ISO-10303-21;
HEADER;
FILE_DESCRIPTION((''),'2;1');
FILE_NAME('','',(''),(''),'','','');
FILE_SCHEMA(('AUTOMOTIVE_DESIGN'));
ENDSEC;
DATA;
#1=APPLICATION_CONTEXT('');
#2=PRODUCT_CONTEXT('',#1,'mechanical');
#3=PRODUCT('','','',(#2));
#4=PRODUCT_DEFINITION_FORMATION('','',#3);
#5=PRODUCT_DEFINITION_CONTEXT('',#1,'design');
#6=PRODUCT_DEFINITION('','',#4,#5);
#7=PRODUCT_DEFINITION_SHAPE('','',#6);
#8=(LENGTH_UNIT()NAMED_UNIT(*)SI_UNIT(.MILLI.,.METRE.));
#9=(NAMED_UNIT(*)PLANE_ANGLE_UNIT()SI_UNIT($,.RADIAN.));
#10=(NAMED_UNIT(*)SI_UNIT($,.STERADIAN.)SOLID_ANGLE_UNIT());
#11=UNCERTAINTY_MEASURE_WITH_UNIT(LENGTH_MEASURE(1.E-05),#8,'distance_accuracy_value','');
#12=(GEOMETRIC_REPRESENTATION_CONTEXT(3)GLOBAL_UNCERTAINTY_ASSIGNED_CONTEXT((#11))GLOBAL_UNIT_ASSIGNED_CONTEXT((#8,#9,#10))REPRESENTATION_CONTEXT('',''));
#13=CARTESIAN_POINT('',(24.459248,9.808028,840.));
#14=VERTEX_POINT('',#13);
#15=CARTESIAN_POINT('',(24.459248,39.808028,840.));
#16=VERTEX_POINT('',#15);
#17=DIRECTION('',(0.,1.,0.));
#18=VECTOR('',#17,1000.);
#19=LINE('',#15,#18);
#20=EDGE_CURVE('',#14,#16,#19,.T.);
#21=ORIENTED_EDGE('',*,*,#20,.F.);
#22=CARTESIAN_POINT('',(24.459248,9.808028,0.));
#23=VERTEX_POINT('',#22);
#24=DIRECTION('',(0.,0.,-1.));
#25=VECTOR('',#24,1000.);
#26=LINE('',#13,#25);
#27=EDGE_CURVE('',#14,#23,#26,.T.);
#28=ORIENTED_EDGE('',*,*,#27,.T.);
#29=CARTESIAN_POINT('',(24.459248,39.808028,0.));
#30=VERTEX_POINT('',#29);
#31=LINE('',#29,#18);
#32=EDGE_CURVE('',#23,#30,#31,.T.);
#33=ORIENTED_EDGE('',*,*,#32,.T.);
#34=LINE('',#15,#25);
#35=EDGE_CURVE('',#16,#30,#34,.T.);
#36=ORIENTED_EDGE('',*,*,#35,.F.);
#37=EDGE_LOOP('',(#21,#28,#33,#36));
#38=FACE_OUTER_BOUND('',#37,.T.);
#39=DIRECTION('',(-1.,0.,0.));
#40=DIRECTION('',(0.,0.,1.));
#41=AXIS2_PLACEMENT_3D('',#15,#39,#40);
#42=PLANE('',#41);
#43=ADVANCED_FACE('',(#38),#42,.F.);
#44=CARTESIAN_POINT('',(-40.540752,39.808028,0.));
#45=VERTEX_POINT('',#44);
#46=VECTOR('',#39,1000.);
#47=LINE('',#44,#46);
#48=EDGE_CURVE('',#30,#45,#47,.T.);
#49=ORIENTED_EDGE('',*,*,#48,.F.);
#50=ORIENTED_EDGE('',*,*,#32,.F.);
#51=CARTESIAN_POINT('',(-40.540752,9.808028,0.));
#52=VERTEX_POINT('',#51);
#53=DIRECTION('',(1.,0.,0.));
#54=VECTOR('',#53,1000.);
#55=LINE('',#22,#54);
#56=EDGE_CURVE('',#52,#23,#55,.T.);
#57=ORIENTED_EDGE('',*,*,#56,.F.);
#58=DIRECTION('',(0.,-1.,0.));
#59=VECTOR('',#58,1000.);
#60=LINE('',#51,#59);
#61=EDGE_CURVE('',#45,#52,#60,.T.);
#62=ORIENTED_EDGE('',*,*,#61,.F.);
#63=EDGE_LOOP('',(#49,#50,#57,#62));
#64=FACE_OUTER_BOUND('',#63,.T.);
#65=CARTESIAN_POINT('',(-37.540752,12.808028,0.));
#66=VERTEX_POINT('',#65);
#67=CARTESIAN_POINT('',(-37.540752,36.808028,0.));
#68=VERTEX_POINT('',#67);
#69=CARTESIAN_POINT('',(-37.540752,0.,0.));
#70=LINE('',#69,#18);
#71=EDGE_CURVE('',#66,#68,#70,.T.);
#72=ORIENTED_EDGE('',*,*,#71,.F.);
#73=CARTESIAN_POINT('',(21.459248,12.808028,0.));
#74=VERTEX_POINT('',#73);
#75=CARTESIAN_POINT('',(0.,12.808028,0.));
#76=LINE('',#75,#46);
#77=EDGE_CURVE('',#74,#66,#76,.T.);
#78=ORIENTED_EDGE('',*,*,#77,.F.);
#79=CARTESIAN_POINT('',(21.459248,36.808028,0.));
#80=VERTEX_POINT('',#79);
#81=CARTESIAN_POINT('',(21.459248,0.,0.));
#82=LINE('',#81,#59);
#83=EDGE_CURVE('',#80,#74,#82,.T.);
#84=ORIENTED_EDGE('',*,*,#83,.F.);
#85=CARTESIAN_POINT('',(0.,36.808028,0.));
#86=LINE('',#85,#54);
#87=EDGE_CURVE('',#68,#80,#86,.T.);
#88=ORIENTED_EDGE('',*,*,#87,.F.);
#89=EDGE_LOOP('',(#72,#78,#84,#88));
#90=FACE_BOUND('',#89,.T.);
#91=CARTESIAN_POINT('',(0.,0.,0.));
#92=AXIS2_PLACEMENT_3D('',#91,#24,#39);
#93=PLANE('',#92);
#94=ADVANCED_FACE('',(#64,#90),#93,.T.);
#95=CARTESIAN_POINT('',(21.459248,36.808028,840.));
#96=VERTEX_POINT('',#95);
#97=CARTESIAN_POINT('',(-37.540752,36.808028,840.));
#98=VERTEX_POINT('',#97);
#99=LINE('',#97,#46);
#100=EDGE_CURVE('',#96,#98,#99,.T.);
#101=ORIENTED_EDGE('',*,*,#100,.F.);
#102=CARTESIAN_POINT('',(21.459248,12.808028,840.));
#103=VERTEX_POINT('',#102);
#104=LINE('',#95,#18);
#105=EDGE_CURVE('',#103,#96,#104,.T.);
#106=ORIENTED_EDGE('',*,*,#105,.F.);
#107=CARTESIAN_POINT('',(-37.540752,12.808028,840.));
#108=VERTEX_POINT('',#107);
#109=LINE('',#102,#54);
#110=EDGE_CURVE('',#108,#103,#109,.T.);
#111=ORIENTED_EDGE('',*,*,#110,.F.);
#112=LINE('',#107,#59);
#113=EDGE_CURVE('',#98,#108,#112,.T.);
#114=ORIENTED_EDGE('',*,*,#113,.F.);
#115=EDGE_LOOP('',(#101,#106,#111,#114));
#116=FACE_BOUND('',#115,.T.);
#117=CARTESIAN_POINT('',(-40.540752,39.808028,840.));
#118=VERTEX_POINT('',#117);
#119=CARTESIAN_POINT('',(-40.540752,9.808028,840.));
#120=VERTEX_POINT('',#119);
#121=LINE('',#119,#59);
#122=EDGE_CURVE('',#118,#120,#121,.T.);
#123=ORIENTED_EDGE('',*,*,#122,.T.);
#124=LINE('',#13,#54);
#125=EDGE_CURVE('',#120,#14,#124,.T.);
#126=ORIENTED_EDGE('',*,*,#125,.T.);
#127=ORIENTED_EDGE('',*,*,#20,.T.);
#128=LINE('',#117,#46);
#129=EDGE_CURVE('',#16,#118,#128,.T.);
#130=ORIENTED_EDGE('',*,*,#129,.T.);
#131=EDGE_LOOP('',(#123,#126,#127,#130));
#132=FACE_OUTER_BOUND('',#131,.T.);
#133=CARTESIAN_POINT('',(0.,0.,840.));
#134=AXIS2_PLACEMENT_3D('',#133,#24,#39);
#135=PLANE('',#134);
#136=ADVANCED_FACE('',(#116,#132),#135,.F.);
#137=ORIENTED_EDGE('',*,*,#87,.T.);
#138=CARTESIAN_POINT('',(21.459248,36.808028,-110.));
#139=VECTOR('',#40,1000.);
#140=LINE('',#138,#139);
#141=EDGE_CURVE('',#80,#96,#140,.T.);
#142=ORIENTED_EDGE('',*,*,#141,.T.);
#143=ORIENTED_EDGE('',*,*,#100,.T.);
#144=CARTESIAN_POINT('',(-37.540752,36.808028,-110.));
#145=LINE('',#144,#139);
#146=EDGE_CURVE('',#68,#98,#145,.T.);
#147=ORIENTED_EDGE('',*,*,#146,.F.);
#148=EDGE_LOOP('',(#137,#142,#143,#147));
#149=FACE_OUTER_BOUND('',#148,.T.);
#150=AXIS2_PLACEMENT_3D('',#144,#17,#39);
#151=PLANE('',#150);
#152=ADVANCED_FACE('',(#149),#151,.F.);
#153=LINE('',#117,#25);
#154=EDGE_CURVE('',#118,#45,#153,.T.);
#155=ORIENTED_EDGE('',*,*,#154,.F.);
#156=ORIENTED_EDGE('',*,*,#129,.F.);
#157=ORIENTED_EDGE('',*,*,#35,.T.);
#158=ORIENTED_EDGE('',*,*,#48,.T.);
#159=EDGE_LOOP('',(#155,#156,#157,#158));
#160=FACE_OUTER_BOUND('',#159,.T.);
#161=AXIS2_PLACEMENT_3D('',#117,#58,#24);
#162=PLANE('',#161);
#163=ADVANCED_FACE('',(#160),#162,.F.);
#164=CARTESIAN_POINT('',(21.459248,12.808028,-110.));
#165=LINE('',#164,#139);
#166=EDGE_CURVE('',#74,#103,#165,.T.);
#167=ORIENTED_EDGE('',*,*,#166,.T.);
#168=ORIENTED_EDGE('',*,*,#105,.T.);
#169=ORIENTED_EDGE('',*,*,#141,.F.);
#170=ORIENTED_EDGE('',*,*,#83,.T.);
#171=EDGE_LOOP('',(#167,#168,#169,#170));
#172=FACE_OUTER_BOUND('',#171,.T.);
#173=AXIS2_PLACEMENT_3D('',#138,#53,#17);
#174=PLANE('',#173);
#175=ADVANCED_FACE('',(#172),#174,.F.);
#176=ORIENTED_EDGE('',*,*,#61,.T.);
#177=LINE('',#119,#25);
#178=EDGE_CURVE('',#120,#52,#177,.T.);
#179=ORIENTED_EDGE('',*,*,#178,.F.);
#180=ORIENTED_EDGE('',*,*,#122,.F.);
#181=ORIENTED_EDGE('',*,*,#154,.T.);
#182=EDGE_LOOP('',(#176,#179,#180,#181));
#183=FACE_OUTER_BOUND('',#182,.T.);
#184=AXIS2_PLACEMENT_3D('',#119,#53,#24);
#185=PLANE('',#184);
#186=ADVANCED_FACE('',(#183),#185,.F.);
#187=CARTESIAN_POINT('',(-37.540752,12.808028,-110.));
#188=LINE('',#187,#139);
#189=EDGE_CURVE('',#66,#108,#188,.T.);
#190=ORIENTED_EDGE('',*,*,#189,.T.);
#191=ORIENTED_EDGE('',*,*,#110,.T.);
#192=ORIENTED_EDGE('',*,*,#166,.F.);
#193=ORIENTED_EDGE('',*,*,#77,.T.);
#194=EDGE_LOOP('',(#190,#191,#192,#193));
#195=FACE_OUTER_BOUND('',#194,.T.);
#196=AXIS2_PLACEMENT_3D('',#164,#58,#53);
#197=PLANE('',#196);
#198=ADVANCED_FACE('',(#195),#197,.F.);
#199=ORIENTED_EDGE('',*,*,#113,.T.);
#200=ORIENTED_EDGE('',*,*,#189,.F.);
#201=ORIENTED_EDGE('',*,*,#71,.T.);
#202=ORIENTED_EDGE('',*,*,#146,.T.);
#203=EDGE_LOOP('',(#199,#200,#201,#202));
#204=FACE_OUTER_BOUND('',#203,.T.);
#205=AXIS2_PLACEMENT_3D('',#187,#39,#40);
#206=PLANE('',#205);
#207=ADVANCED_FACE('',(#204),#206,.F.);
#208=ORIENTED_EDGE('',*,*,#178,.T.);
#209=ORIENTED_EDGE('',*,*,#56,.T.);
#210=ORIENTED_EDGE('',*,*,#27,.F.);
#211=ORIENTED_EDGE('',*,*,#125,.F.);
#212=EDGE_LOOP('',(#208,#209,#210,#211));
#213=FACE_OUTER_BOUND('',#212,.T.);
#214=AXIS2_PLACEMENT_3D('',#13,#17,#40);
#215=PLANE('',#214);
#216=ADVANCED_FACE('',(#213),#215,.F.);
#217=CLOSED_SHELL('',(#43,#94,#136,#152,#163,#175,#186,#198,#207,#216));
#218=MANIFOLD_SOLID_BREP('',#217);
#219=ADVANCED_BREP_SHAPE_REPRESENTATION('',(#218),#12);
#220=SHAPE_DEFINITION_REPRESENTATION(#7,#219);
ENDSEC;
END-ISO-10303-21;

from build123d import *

# Parameters (mm, degrees)
SKETCH1_W           = 65
SKETCH1_H           = 30
BOSS_EXTRUDE1_DEPTH = 840
SKETCH2_W           = 59
SKETCH2_H           = 24
CUT_EXTRUDE1_DEPTH  = 950


with BuildPart() as part:
    # Sketch1 → Boss-Extrude1 (new body)
    with BuildSketch(Plane.XY):
        with Locations((-8.040751589, 24.808027615)):
            Rectangle(SKETCH1_W, SKETCH1_H)
    extrude(amount=BOSS_EXTRUDE1_DEPTH)

    # Sketch2 → Cut-Extrude1 (cut)
    with BuildSketch(Plane.XY.offset(840)):
        with Locations((-8.040751589, 24.808027615)):
            Rectangle(SKETCH2_W, SKETCH2_H)
    extrude(amount=-CUT_EXTRUDE1_DEPTH, mode=Mode.SUBTRACT)


solid = part.part
